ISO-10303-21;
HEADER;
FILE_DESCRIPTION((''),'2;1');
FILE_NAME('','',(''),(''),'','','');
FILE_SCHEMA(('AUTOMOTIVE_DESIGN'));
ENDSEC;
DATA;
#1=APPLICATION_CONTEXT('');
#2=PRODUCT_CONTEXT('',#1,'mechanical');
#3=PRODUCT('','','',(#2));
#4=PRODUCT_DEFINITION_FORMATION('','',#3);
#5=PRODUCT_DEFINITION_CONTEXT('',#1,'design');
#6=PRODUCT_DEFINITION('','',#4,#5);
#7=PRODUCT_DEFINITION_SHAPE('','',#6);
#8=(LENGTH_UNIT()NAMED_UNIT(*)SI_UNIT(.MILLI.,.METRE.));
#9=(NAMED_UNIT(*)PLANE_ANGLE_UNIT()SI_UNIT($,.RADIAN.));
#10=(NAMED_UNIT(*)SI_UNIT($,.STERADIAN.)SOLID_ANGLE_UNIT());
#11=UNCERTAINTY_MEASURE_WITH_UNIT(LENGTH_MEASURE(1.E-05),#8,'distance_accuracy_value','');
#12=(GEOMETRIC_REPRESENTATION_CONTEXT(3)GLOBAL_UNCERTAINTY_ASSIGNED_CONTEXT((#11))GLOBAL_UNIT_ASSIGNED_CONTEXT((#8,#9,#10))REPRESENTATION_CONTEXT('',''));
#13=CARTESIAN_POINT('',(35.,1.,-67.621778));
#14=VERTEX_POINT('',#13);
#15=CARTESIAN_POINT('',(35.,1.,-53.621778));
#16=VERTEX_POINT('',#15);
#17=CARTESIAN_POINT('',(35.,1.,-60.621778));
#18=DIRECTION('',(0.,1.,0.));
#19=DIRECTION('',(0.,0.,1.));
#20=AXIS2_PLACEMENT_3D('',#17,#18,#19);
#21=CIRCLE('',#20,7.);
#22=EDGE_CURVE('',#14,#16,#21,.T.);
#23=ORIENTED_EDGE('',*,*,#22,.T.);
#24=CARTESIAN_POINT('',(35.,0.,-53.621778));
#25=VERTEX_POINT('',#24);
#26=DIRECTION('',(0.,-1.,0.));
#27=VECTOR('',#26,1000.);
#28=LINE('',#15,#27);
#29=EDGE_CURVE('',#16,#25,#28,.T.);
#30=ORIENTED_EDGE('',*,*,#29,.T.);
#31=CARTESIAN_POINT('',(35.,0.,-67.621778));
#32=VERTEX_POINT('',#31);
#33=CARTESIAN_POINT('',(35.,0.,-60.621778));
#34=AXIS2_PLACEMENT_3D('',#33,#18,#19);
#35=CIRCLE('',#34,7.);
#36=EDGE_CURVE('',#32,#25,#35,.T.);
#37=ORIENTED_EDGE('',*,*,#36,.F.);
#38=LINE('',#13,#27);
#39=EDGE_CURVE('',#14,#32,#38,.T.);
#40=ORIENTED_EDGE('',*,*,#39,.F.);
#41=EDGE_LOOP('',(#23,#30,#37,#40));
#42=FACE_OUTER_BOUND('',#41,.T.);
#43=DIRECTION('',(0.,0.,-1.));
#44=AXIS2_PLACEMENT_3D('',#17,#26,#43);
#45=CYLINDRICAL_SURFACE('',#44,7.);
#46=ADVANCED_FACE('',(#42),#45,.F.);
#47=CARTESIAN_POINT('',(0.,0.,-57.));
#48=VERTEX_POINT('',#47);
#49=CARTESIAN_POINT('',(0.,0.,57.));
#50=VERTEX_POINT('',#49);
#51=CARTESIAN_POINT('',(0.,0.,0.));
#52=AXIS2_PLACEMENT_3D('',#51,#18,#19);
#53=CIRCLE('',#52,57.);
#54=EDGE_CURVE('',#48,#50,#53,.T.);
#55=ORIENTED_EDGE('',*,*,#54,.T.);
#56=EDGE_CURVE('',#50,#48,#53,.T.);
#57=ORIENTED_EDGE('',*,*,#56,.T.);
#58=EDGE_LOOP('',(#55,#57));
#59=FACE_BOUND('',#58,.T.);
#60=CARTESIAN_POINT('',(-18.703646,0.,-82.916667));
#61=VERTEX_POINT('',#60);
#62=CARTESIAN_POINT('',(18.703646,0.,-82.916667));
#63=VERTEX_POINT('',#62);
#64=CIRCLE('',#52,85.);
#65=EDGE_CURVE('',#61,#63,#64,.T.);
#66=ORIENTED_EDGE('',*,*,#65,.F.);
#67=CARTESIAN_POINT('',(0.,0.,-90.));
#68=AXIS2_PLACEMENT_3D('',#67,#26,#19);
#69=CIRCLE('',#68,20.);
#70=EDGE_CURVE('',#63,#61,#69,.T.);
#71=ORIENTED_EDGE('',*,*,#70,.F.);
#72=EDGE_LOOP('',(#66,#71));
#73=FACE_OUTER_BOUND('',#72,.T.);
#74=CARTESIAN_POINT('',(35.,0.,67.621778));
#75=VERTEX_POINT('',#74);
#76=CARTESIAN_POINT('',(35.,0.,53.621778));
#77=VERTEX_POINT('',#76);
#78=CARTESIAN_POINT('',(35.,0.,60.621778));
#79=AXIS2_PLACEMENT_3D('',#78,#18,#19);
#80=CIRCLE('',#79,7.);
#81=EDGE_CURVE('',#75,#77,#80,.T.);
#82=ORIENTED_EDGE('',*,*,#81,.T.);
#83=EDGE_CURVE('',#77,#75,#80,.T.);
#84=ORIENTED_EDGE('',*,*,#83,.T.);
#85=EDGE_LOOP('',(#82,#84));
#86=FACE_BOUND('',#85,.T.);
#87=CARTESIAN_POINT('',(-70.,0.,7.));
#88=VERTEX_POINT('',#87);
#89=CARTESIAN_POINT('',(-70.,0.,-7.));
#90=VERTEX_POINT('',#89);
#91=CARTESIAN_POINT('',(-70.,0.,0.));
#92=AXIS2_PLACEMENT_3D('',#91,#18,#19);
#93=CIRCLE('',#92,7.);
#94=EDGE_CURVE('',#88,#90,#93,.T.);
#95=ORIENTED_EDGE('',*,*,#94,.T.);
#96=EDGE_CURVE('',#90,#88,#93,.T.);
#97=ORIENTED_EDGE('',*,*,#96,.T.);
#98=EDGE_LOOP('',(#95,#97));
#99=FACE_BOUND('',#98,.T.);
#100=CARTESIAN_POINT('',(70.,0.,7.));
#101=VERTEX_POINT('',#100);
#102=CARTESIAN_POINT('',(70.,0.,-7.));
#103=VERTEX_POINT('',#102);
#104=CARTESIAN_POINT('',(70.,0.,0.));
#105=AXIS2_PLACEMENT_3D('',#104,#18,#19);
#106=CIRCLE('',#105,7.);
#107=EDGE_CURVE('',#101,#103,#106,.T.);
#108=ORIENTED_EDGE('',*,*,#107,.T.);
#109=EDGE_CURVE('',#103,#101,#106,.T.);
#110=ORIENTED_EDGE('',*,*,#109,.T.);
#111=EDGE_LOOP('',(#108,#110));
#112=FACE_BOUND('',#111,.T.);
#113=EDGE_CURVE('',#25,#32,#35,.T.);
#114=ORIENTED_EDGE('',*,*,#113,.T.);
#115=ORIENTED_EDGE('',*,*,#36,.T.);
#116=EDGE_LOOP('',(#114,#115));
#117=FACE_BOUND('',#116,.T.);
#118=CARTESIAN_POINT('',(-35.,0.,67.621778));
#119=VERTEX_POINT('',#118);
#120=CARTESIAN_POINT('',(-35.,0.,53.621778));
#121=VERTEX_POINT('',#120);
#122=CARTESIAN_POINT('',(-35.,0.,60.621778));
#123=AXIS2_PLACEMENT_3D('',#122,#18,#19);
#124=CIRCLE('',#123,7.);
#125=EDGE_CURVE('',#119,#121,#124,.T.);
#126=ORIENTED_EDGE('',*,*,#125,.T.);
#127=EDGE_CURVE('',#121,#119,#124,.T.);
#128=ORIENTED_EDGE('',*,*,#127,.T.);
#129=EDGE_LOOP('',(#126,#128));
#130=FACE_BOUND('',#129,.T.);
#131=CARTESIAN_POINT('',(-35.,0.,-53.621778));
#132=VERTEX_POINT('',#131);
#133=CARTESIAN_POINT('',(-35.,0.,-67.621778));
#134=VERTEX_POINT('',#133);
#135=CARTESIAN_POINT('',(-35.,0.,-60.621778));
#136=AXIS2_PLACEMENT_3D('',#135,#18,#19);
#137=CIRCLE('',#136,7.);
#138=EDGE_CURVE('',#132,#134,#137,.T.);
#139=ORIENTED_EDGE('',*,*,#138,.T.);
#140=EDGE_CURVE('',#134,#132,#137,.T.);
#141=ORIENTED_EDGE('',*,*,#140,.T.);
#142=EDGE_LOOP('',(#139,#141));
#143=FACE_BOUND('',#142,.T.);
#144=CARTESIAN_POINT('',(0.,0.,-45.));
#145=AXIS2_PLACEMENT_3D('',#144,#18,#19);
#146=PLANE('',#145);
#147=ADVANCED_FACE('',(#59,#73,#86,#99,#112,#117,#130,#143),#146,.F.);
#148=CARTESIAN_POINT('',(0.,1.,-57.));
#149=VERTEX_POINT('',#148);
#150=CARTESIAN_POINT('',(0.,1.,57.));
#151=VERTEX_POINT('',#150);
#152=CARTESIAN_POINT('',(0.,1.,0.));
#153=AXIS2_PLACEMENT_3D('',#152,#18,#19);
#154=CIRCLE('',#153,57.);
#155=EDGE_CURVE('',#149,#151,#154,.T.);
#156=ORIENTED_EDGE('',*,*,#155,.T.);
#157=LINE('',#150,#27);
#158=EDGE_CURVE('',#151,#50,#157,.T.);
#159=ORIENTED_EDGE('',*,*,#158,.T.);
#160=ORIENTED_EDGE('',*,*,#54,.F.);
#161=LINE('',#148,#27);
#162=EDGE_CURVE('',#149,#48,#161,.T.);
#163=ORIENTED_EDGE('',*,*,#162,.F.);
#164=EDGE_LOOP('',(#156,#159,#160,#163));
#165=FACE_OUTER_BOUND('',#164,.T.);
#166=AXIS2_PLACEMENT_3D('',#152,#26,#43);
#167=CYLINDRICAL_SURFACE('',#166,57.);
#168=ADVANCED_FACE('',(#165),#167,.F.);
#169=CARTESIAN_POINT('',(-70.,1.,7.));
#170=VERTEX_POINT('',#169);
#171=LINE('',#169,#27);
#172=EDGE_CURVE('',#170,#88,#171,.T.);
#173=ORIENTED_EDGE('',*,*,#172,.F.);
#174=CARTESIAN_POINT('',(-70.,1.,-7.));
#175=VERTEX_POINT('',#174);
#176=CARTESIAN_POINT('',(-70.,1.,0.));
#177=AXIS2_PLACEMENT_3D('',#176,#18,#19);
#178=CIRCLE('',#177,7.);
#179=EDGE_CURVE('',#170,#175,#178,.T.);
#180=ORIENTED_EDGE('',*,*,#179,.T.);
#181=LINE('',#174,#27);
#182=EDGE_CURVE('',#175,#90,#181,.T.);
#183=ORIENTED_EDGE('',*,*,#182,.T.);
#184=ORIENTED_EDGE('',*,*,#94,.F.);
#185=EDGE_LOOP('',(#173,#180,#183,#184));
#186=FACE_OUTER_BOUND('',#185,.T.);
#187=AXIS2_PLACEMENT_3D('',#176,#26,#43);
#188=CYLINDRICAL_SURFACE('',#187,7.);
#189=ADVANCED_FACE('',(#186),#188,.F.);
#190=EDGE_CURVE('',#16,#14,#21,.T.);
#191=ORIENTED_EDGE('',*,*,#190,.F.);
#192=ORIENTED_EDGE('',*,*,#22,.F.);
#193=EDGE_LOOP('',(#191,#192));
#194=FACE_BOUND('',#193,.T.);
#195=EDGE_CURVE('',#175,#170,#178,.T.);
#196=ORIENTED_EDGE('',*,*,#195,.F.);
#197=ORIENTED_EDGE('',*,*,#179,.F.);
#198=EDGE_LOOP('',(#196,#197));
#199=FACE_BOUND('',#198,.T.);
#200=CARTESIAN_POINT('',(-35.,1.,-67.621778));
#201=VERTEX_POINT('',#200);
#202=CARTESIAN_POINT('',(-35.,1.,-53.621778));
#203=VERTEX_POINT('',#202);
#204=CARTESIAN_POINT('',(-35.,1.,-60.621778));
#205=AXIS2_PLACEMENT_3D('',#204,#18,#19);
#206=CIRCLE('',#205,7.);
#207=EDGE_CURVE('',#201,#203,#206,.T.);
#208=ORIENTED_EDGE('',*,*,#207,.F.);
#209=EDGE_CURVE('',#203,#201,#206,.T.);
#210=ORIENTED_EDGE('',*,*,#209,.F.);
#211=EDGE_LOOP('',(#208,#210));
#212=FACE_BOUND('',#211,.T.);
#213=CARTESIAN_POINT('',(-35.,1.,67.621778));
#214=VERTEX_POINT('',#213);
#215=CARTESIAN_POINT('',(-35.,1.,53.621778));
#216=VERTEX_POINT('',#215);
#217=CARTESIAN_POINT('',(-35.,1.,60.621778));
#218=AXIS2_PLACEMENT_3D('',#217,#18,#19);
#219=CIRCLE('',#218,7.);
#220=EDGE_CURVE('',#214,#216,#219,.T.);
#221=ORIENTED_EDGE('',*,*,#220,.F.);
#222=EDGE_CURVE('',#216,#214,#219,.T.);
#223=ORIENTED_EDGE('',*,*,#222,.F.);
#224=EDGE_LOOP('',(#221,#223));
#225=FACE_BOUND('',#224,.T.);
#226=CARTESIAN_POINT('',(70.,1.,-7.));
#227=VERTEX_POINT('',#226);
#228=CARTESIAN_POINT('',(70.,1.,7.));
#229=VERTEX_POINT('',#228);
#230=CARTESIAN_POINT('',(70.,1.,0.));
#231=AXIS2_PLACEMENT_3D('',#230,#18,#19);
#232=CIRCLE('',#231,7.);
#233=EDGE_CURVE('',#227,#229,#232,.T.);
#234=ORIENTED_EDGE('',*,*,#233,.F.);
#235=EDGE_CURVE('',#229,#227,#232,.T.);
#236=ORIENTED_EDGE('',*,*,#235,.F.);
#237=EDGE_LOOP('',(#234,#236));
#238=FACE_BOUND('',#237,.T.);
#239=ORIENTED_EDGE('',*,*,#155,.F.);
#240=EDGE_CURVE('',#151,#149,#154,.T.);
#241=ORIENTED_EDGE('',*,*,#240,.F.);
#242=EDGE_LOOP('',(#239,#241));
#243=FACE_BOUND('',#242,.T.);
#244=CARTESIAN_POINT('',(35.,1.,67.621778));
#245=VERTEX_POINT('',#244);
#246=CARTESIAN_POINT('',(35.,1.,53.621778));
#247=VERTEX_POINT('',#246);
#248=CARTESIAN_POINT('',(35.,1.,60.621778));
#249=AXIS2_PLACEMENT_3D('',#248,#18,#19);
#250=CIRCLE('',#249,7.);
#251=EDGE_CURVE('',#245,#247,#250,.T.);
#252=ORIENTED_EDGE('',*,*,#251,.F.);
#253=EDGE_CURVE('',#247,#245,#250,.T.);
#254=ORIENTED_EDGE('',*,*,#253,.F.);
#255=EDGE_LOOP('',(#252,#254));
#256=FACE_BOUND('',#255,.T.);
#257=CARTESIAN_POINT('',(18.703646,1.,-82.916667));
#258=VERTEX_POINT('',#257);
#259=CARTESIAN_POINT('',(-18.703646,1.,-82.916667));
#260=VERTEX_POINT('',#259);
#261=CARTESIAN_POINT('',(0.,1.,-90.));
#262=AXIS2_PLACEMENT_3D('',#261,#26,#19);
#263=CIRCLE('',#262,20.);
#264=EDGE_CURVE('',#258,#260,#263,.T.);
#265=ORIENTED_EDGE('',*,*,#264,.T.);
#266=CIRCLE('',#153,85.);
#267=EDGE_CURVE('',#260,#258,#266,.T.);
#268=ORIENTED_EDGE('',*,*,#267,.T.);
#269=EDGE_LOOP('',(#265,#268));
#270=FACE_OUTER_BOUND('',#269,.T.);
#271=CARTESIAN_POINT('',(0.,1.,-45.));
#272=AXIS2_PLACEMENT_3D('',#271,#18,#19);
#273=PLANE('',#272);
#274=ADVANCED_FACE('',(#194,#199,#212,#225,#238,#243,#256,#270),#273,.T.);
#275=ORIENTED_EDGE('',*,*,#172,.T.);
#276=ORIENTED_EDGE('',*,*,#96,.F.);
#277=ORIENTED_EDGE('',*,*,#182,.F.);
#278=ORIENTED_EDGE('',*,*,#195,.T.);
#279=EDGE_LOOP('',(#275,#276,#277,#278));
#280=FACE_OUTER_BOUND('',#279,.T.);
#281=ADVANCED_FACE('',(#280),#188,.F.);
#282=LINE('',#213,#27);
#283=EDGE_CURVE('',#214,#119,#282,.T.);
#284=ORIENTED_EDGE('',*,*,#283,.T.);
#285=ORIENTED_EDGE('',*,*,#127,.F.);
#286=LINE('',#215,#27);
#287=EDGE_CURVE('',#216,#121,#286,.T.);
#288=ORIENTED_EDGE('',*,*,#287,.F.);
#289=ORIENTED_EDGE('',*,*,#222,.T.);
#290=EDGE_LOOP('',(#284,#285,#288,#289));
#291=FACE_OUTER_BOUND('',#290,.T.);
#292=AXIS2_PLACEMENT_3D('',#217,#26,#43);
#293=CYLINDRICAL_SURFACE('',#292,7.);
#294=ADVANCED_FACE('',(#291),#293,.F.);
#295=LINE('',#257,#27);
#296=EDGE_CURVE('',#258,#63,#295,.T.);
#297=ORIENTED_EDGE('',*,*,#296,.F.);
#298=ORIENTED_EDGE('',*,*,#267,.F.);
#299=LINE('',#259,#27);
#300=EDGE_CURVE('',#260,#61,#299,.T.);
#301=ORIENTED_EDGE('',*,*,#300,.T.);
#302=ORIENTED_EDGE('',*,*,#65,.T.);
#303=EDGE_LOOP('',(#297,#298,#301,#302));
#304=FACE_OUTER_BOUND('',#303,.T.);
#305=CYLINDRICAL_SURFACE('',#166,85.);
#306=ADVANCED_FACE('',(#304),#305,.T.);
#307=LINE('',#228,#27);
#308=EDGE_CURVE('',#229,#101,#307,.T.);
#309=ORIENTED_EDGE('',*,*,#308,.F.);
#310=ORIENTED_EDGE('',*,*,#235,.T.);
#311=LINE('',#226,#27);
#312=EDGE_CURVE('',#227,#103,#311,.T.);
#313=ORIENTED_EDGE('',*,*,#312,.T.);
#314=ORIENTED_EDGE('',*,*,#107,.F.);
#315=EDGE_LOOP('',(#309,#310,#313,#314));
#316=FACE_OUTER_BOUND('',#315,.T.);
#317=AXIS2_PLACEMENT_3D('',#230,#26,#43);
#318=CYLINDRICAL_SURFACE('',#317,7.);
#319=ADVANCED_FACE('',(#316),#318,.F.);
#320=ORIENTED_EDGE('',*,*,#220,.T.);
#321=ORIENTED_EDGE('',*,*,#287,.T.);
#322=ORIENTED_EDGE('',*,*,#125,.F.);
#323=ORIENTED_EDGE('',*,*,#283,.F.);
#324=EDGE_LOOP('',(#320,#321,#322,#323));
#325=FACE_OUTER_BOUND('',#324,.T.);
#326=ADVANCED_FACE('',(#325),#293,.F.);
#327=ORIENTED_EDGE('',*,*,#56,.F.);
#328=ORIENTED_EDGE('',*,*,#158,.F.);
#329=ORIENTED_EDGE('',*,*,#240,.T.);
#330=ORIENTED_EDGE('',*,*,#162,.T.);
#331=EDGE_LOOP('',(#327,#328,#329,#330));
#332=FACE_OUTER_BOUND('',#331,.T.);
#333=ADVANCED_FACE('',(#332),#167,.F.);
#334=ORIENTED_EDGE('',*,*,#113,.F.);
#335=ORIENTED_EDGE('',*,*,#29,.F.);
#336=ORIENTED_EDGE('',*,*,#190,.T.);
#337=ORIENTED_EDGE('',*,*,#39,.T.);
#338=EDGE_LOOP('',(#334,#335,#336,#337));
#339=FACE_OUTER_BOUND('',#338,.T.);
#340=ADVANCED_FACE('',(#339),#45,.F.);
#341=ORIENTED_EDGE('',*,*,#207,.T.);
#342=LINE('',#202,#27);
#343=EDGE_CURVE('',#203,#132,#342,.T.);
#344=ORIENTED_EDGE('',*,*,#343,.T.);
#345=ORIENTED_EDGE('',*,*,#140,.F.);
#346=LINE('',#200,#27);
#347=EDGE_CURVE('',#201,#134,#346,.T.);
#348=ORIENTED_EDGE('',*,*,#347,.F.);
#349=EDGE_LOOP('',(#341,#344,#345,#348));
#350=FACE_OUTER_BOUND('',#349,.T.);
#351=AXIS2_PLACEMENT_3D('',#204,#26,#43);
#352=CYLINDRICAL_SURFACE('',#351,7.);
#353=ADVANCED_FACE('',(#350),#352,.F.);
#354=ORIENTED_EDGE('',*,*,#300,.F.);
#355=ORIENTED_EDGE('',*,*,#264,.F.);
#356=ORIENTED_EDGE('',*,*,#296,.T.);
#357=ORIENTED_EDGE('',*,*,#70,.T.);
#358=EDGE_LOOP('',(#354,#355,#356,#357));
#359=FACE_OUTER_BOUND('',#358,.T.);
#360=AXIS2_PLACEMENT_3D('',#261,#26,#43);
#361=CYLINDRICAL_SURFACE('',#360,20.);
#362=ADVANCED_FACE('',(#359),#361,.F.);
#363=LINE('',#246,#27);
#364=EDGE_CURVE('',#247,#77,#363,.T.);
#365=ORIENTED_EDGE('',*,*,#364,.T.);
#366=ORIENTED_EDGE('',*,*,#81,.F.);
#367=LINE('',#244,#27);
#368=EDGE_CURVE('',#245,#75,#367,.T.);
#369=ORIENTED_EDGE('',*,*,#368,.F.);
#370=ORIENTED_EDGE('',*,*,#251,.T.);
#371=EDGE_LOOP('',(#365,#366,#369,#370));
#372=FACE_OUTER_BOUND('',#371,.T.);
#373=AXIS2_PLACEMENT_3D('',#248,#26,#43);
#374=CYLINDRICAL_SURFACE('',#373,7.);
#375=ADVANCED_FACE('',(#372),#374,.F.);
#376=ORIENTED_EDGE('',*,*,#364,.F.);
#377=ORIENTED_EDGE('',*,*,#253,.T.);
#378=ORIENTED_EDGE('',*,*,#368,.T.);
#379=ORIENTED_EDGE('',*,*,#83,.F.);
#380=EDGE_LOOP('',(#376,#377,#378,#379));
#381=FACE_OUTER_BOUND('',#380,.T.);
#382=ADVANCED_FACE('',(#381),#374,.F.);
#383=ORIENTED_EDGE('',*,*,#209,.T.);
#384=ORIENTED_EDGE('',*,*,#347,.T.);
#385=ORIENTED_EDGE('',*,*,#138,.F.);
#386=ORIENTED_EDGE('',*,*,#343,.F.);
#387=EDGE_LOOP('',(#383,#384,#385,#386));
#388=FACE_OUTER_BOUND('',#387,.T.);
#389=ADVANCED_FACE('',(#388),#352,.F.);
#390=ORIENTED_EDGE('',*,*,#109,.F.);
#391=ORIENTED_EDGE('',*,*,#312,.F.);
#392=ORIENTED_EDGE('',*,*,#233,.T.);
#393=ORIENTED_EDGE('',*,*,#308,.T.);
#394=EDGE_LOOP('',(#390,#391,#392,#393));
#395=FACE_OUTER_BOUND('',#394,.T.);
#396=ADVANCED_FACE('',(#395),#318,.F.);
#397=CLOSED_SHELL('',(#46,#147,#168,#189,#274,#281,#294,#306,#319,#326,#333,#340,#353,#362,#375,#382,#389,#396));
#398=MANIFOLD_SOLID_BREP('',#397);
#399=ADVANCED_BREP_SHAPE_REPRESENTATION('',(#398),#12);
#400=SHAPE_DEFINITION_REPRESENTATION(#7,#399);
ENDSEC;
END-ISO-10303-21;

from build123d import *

# Parameters (mm, degrees)
SKETCH1_R           = 7
SKETCH1_R_2         = 57
BOSS_EXTRUDE1_DEPTH = 1


with BuildPart() as part:
    # Sketch1 → Boss-Extrude1 (new body)
    with BuildSketch(Plane(origin=(0, 0, 0), x_dir=(1, 0, 0), z_dir=(0, 1, 0))):
        with BuildLine():
            ThreePointArc((-18.703646406, 82.916666667), (0, -85), (18.703646406, 82.916666667))
            ThreePointArc((18.703646406, 82.916666667), (0, 70), (-18.703646406, 82.916666667))
        make_face()
        with Locations(Location((-35, 60.621778265, 0), (0, 0, 270))):
            Circle(SKETCH1_R, mode=Mode.SUBTRACT)
        with Locations(Location((35, 60.621778265, 0), (0, 0, 270))):
            Circle(SKETCH1_R, mode=Mode.SUBTRACT)
        with Locations(Location((70, 0, 0), (0, 0, 270))):
            Circle(SKETCH1_R, mode=Mode.SUBTRACT)
        with Locations(Location((35, -60.621778265, 0), (0, 0, 270))):
            Circle(SKETCH1_R, mode=Mode.SUBTRACT)
        with Locations(Location((-35, -60.621778265, 0), (0, 0, 270))):
            Circle(SKETCH1_R, mode=Mode.SUBTRACT)
        with Locations(Location((-70, 0, 0), (0, 0, 270))):
            Circle(SKETCH1_R, mode=Mode.SUBTRACT)
        with Locations(Location((0, 0, 0), (0, 0, 270))):
            Circle(SKETCH1_R_2, mode=Mode.SUBTRACT)
    extrude(amount=BOSS_EXTRUDE1_DEPTH)


solid = part.part
